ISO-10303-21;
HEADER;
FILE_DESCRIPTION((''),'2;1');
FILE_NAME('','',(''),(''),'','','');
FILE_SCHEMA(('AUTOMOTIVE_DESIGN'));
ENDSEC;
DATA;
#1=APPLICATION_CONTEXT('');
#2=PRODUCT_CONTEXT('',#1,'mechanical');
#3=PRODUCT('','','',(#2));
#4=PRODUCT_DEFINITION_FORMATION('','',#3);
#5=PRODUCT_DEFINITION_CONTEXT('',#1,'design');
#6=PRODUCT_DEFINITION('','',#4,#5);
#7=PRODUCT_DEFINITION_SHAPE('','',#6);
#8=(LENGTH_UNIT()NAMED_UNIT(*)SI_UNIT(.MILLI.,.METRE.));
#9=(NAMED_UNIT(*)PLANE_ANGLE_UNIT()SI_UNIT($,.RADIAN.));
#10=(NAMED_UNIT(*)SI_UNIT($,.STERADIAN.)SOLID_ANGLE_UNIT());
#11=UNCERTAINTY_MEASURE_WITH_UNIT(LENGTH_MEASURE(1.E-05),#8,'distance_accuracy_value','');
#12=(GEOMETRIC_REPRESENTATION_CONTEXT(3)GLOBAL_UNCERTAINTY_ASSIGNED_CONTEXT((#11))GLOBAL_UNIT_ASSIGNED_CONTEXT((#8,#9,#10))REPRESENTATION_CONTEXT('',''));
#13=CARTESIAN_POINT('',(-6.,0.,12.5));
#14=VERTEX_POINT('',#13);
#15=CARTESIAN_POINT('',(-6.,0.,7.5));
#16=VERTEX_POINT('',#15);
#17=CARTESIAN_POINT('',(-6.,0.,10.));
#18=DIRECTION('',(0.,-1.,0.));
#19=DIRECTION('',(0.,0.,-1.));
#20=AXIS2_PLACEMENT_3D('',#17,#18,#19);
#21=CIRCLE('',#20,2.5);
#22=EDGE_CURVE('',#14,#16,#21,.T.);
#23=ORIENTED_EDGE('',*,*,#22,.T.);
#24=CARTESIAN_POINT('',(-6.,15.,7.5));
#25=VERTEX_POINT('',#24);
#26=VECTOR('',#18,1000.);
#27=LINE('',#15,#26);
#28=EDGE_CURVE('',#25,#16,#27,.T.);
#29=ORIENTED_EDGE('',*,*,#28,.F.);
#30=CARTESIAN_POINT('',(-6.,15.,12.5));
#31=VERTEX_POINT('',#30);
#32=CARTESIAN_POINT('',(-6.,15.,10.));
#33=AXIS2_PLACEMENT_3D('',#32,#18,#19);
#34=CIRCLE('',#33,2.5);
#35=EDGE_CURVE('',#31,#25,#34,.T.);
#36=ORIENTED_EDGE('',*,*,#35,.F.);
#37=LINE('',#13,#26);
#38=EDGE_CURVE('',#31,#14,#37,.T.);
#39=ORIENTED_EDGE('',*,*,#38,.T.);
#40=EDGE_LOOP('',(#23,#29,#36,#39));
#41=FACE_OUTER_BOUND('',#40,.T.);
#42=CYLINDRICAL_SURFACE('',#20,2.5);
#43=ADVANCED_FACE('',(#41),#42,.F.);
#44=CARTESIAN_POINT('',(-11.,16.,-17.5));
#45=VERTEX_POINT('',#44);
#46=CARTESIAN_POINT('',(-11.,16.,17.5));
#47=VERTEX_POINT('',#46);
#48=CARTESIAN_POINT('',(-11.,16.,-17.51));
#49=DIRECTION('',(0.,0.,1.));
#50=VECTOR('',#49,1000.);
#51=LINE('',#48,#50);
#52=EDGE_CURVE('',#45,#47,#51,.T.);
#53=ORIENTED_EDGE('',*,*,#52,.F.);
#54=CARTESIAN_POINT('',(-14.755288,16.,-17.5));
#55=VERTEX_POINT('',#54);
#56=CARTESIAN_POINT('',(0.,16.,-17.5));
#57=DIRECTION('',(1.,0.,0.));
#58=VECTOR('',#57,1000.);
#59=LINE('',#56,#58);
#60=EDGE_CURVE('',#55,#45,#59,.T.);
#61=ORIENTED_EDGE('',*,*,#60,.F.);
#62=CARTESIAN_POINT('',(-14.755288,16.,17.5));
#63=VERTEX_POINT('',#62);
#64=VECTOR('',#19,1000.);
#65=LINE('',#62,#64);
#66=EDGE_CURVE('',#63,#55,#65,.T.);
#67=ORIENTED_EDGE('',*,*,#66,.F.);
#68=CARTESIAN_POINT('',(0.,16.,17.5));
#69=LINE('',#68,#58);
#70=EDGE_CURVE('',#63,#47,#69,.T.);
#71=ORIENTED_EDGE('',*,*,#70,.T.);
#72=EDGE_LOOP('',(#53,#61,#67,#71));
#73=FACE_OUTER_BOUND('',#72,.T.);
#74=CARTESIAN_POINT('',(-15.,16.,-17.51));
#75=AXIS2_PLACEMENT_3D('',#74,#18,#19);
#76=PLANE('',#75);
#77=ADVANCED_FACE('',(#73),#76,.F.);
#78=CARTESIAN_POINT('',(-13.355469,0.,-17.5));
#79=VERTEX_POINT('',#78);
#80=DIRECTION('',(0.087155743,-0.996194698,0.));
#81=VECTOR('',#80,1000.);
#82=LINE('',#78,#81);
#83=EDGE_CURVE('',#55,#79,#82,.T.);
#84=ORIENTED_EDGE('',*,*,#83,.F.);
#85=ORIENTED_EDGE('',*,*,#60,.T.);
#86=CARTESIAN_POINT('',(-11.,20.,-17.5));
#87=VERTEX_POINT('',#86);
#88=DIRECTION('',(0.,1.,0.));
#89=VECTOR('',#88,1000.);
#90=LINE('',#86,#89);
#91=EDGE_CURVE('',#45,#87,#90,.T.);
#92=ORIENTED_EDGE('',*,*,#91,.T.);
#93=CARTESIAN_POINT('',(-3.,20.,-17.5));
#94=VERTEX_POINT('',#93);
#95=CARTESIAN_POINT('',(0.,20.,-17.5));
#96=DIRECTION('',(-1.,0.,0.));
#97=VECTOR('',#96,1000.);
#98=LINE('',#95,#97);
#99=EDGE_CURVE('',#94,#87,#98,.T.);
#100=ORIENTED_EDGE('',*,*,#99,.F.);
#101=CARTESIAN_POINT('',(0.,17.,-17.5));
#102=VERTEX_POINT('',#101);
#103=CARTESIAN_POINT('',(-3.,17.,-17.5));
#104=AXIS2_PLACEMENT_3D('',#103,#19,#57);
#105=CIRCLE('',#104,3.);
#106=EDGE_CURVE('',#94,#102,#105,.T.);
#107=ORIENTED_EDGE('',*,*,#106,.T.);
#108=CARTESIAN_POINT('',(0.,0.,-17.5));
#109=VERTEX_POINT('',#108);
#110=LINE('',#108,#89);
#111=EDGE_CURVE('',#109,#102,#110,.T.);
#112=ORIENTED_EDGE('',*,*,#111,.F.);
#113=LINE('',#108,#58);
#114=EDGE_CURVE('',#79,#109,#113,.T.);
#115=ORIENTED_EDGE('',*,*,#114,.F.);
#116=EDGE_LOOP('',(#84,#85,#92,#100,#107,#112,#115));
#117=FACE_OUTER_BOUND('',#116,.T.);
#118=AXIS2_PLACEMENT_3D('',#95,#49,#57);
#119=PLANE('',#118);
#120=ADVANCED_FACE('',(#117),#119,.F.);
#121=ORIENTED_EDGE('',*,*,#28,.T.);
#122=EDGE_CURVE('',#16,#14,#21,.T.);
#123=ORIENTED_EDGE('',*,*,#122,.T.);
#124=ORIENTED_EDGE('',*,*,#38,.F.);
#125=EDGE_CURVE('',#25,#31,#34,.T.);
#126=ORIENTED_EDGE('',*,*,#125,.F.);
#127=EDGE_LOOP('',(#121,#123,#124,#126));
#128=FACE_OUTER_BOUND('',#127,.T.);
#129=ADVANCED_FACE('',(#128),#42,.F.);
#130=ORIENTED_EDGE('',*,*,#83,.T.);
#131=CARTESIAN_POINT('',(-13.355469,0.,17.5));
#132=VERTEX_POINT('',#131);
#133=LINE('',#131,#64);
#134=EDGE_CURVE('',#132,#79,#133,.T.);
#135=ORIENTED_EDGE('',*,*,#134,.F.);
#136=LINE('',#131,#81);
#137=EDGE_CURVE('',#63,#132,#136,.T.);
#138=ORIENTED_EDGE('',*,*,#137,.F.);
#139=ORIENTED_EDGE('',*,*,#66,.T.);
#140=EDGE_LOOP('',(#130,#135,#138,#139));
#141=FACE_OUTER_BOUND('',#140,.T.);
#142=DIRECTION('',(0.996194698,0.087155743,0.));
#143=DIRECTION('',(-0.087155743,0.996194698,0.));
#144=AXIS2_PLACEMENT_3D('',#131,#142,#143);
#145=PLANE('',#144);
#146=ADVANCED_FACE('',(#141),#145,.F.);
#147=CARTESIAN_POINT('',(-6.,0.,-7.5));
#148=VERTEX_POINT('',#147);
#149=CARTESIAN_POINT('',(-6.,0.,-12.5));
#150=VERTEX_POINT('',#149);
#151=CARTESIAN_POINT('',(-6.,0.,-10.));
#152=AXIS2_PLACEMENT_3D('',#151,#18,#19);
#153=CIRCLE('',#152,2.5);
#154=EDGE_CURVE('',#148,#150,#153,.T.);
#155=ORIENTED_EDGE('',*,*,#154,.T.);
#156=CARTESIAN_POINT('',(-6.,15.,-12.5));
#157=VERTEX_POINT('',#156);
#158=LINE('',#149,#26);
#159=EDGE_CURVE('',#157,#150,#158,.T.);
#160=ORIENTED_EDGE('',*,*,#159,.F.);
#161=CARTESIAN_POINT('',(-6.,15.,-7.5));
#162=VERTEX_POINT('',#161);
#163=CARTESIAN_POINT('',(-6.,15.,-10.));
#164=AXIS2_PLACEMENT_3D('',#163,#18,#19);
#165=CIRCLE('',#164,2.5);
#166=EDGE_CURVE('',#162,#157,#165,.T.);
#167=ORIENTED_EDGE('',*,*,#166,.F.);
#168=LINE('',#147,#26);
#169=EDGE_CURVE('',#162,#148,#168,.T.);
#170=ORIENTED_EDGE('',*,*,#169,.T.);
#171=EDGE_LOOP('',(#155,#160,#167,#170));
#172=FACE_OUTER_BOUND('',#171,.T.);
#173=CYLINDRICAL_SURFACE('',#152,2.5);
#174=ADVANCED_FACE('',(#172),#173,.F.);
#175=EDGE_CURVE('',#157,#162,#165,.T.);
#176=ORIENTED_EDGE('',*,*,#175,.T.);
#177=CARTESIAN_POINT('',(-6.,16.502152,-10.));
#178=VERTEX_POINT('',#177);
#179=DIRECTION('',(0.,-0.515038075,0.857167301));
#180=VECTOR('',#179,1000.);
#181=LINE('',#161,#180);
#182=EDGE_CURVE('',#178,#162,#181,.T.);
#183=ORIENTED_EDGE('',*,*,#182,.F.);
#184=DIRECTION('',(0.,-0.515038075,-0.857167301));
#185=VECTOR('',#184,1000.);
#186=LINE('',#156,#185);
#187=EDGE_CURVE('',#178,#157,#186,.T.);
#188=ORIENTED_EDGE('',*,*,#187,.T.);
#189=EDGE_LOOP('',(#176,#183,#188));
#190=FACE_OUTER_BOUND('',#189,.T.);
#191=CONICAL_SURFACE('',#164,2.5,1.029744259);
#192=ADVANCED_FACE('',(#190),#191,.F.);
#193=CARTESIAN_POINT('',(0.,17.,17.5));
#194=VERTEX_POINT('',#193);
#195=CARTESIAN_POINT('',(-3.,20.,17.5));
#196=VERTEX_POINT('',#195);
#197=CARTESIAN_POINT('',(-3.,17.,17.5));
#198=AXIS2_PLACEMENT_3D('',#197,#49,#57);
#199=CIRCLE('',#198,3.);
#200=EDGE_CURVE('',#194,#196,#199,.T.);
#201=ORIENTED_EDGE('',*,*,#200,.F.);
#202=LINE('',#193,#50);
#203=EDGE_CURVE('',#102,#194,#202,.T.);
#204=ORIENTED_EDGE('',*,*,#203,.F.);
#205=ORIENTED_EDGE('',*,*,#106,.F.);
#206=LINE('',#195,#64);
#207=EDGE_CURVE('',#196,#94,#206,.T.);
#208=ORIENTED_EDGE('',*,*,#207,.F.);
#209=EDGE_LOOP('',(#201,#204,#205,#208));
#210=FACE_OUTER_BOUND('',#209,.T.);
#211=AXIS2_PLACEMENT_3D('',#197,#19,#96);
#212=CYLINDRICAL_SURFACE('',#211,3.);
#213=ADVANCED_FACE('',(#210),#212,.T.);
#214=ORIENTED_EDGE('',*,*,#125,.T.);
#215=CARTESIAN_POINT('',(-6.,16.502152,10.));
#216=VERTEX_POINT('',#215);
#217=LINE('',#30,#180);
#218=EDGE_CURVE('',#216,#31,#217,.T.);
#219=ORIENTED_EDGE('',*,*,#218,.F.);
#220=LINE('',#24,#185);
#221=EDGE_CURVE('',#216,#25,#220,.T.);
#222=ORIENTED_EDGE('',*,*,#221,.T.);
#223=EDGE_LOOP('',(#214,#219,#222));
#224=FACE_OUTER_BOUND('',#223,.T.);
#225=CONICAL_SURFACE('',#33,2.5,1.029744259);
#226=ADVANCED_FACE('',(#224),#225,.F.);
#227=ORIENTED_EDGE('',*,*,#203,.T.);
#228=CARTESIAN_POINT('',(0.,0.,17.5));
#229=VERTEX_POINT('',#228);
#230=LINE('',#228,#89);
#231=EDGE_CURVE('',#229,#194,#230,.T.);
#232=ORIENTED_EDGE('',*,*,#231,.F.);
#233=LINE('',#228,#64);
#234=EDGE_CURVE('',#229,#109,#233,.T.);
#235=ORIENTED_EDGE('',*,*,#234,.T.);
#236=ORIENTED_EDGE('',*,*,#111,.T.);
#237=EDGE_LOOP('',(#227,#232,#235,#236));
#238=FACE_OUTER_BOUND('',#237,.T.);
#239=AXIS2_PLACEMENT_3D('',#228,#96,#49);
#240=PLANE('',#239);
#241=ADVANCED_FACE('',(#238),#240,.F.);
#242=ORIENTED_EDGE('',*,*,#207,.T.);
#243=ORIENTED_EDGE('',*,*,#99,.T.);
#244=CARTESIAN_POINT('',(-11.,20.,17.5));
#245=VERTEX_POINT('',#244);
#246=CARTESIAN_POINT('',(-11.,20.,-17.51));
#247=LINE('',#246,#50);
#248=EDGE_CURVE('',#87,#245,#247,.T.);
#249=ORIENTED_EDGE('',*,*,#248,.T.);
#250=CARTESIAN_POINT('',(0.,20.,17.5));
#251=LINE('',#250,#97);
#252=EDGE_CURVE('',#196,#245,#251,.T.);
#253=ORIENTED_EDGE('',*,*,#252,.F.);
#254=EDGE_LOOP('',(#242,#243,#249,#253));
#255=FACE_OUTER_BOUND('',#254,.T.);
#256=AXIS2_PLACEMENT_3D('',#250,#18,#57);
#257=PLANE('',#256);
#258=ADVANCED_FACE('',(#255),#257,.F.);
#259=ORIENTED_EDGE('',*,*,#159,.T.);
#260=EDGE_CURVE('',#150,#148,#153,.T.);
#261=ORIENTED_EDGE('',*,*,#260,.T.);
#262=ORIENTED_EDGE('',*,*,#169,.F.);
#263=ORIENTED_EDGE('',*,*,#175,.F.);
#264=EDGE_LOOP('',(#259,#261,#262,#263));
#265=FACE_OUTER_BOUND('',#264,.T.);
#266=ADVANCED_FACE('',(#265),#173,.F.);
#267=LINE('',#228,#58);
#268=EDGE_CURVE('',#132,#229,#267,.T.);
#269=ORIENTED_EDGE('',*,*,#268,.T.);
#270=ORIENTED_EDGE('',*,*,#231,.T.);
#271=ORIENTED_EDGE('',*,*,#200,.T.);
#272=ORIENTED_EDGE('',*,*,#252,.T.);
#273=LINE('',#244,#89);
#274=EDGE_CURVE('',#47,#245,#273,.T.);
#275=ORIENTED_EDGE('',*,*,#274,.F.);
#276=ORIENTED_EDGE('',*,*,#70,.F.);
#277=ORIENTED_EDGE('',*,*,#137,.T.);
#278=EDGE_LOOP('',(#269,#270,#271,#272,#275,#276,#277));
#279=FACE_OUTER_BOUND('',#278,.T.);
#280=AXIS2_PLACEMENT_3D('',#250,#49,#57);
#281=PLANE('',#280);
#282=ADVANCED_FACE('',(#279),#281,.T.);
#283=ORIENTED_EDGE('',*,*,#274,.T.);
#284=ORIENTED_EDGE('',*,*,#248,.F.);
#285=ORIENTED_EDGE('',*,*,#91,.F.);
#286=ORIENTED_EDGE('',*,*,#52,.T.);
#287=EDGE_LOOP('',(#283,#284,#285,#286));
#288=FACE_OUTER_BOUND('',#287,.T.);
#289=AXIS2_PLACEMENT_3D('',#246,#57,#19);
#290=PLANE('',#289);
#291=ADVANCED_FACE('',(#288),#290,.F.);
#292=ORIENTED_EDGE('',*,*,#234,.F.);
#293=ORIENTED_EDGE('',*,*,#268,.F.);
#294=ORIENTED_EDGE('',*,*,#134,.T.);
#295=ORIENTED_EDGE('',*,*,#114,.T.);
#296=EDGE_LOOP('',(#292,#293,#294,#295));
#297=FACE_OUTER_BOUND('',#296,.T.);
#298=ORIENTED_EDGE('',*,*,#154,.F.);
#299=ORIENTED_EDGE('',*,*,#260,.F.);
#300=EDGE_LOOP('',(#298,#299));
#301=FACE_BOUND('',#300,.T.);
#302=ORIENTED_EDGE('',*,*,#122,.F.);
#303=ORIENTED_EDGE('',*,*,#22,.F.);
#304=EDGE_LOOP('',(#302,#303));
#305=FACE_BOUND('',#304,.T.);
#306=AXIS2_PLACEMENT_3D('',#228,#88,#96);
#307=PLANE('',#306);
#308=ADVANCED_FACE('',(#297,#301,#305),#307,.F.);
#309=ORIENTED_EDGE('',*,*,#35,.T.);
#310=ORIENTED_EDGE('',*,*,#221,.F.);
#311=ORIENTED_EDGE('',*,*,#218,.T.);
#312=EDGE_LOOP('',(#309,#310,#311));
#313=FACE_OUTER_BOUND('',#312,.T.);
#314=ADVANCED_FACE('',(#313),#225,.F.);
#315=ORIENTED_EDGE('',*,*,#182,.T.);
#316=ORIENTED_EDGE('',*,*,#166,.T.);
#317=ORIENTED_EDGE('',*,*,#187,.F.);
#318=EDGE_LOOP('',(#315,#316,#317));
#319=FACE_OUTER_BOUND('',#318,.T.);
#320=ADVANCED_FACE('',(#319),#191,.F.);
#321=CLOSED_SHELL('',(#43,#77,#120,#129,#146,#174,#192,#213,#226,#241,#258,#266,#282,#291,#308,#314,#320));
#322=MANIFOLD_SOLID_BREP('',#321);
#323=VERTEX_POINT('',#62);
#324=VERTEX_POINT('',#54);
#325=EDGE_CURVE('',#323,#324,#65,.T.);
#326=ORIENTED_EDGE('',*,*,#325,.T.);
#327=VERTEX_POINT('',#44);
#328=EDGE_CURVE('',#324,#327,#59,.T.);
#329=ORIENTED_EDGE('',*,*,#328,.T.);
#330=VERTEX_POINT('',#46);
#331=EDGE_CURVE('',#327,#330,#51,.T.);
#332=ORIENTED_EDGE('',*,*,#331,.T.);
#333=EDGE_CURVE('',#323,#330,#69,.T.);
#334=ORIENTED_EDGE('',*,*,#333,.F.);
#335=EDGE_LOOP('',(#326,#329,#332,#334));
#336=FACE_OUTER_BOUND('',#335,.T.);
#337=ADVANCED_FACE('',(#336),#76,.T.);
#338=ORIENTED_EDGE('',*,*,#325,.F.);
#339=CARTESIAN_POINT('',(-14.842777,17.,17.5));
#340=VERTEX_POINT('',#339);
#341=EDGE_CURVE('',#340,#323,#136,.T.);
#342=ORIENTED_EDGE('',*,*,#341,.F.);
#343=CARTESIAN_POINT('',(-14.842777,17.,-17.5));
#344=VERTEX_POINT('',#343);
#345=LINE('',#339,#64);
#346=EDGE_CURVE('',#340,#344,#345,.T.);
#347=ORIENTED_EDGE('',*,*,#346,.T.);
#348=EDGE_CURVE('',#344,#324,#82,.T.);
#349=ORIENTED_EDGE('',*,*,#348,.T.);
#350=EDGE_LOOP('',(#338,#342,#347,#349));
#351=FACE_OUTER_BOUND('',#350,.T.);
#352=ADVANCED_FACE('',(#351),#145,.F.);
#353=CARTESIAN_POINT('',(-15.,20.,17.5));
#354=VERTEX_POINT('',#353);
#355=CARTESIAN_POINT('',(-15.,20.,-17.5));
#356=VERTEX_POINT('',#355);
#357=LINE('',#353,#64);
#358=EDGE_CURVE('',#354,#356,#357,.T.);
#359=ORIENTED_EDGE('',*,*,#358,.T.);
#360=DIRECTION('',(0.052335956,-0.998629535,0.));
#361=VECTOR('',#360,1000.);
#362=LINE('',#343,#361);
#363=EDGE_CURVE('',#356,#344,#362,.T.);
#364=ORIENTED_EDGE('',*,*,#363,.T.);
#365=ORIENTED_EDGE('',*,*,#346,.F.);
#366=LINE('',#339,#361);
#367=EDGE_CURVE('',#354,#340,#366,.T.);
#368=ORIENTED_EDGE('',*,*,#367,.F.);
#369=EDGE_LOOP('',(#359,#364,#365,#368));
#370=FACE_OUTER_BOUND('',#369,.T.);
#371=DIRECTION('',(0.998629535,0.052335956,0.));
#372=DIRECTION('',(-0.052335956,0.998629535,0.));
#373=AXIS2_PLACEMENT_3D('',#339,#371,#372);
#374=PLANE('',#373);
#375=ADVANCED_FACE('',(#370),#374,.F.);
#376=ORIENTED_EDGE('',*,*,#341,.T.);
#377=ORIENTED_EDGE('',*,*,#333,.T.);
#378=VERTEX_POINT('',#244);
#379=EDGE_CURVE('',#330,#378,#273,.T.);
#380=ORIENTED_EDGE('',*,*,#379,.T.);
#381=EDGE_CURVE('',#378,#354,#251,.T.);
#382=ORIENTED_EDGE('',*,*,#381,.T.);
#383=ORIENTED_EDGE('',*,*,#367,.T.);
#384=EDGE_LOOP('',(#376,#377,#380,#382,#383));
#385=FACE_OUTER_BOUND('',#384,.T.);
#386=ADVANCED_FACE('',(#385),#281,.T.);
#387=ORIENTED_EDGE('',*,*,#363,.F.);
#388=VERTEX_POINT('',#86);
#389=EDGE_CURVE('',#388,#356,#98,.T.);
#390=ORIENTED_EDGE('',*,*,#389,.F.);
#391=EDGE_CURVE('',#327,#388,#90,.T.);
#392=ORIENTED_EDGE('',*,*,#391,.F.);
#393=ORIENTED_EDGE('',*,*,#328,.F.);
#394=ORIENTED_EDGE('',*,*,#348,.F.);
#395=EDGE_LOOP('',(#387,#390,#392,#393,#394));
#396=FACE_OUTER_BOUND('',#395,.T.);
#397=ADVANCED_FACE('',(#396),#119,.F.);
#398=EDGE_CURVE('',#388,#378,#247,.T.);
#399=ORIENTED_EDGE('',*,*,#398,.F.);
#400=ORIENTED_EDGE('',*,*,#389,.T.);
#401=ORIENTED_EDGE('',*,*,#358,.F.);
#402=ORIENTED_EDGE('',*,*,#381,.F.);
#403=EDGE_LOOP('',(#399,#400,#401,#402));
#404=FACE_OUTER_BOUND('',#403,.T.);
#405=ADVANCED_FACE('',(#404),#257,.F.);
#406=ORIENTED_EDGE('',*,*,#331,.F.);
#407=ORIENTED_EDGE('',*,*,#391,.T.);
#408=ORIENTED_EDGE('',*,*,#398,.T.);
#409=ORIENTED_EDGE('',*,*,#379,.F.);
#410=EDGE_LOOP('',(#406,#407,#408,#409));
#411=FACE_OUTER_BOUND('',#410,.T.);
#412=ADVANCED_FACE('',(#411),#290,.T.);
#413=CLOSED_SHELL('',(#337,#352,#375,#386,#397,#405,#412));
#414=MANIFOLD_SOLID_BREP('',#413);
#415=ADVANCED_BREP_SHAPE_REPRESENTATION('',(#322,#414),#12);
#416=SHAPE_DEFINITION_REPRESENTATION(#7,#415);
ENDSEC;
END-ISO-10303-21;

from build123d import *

# Parameters (mm, degrees)
BOSS_EXTRUDE1_DEPTH        = 17.5
SPLIT1_SURFACE_1_BACK      = 44.012
SPLIT1_SURFACE_1_DEPTH     = 88.024
SPLIT1_SURFACE_2_BACK      = 44.012
SPLIT1_SURFACE_2_DEPTH     = 88.024
M6_TAPPED_HOLE1_AT_2_COUNT = 2
M6_TAPPED_HOLE1_AT_2_PITCH = 20
FILLET1_R                  = 3


with BuildPart() as part:
    # Sketch1 → Boss-Extrude1 (new, symmetric)
    with BuildSketch(Plane.XY):
        Polygon((-14.842776662, 17), (-15, 20), (0, 20), (0, 0), (-13.355469382, 0), align=None)
    extrude(amount=BOSS_EXTRUDE1_DEPTH, both=True)


with BuildPart() as body_2:
    # Split1: the piece behind the surface
    add(part.part)
    # Split1 surface: a surface, the sketch's curves swept straight by 88.024 mm
    with BuildLine(Plane.XY.offset(17.5).offset(-SPLIT1_SURFACE_1_BACK), mode=Mode.PRIVATE) as split1_surface_1_path:
        Line((-15, 20), (-11, 20))
        Line((-11, 20), (-11, 16))
        Line((-11, 16), (-15, 16))
        Line((-15, 16), (-15, 20))
    split1_surface_1 = Shell.extrude(split1_surface_1_path.wire(), (0 * SPLIT1_SURFACE_1_DEPTH, 0 * SPLIT1_SURFACE_1_DEPTH, 1 * SPLIT1_SURFACE_1_DEPTH))
    split(bisect_by=split1_surface_1, keep=Keep.BOTTOM)


with BuildPart() as part_1:
    add(part.part)

    # Split1: split by a surface, the side it looks to stays
    # Split1 surface: a surface, the sketch's curves swept straight by 88.024 mm
    with BuildLine(Plane.XY.offset(17.5).offset(-SPLIT1_SURFACE_2_BACK), mode=Mode.PRIVATE) as split1_surface_2_path:
        Line((-15, 20), (-11, 20))
        Line((-11, 20), (-11, 16))
        Line((-11, 16), (-15, 16))
        Line((-15, 16), (-15, 20))
    split1_surface_2 = Shell.extrude(split1_surface_2_path.wire(), (0 * SPLIT1_SURFACE_2_DEPTH, 0 * SPLIT1_SURFACE_2_DEPTH, 1 * SPLIT1_SURFACE_2_DEPTH))
    split(bisect_by=split1_surface_2, keep=Keep.TOP)

    # Sketch3 → M6 Tapped Hole1 (revolve, cut)
    with BuildSketch(Plane(origin=(-6, 0, 10), x_dir=(0, 0, -1), z_dir=(1, 0, 0))):
        Polygon((0, 0), (0, 16.502151548), (2.5, 15), (2.5, 0), align=None)
    m6_tapped_hole1 = revolve(axis=Axis((-6, -6.35, 10), (0, 1, 0)), mode=Mode.SUBTRACT)

    # M6 Tapped Hole1 at 2: M6 Tapped Hole1 ×2
    with Locations(*[(0, 0, -i * M6_TAPPED_HOLE1_AT_2_PITCH) for i in range(1, M6_TAPPED_HOLE1_AT_2_COUNT)]):
        add(m6_tapped_hole1, mode=Mode.SUBTRACT)

    # Fillet1
    fillet1_edges = [part_1.edges().sort_by_distance(p)[0] for p in [
        (0, 20, 0),
    ]]
    fillet(fillet1_edges, radius=FILLET1_R)


solid = Compound([body_2.part, part_1.part])
